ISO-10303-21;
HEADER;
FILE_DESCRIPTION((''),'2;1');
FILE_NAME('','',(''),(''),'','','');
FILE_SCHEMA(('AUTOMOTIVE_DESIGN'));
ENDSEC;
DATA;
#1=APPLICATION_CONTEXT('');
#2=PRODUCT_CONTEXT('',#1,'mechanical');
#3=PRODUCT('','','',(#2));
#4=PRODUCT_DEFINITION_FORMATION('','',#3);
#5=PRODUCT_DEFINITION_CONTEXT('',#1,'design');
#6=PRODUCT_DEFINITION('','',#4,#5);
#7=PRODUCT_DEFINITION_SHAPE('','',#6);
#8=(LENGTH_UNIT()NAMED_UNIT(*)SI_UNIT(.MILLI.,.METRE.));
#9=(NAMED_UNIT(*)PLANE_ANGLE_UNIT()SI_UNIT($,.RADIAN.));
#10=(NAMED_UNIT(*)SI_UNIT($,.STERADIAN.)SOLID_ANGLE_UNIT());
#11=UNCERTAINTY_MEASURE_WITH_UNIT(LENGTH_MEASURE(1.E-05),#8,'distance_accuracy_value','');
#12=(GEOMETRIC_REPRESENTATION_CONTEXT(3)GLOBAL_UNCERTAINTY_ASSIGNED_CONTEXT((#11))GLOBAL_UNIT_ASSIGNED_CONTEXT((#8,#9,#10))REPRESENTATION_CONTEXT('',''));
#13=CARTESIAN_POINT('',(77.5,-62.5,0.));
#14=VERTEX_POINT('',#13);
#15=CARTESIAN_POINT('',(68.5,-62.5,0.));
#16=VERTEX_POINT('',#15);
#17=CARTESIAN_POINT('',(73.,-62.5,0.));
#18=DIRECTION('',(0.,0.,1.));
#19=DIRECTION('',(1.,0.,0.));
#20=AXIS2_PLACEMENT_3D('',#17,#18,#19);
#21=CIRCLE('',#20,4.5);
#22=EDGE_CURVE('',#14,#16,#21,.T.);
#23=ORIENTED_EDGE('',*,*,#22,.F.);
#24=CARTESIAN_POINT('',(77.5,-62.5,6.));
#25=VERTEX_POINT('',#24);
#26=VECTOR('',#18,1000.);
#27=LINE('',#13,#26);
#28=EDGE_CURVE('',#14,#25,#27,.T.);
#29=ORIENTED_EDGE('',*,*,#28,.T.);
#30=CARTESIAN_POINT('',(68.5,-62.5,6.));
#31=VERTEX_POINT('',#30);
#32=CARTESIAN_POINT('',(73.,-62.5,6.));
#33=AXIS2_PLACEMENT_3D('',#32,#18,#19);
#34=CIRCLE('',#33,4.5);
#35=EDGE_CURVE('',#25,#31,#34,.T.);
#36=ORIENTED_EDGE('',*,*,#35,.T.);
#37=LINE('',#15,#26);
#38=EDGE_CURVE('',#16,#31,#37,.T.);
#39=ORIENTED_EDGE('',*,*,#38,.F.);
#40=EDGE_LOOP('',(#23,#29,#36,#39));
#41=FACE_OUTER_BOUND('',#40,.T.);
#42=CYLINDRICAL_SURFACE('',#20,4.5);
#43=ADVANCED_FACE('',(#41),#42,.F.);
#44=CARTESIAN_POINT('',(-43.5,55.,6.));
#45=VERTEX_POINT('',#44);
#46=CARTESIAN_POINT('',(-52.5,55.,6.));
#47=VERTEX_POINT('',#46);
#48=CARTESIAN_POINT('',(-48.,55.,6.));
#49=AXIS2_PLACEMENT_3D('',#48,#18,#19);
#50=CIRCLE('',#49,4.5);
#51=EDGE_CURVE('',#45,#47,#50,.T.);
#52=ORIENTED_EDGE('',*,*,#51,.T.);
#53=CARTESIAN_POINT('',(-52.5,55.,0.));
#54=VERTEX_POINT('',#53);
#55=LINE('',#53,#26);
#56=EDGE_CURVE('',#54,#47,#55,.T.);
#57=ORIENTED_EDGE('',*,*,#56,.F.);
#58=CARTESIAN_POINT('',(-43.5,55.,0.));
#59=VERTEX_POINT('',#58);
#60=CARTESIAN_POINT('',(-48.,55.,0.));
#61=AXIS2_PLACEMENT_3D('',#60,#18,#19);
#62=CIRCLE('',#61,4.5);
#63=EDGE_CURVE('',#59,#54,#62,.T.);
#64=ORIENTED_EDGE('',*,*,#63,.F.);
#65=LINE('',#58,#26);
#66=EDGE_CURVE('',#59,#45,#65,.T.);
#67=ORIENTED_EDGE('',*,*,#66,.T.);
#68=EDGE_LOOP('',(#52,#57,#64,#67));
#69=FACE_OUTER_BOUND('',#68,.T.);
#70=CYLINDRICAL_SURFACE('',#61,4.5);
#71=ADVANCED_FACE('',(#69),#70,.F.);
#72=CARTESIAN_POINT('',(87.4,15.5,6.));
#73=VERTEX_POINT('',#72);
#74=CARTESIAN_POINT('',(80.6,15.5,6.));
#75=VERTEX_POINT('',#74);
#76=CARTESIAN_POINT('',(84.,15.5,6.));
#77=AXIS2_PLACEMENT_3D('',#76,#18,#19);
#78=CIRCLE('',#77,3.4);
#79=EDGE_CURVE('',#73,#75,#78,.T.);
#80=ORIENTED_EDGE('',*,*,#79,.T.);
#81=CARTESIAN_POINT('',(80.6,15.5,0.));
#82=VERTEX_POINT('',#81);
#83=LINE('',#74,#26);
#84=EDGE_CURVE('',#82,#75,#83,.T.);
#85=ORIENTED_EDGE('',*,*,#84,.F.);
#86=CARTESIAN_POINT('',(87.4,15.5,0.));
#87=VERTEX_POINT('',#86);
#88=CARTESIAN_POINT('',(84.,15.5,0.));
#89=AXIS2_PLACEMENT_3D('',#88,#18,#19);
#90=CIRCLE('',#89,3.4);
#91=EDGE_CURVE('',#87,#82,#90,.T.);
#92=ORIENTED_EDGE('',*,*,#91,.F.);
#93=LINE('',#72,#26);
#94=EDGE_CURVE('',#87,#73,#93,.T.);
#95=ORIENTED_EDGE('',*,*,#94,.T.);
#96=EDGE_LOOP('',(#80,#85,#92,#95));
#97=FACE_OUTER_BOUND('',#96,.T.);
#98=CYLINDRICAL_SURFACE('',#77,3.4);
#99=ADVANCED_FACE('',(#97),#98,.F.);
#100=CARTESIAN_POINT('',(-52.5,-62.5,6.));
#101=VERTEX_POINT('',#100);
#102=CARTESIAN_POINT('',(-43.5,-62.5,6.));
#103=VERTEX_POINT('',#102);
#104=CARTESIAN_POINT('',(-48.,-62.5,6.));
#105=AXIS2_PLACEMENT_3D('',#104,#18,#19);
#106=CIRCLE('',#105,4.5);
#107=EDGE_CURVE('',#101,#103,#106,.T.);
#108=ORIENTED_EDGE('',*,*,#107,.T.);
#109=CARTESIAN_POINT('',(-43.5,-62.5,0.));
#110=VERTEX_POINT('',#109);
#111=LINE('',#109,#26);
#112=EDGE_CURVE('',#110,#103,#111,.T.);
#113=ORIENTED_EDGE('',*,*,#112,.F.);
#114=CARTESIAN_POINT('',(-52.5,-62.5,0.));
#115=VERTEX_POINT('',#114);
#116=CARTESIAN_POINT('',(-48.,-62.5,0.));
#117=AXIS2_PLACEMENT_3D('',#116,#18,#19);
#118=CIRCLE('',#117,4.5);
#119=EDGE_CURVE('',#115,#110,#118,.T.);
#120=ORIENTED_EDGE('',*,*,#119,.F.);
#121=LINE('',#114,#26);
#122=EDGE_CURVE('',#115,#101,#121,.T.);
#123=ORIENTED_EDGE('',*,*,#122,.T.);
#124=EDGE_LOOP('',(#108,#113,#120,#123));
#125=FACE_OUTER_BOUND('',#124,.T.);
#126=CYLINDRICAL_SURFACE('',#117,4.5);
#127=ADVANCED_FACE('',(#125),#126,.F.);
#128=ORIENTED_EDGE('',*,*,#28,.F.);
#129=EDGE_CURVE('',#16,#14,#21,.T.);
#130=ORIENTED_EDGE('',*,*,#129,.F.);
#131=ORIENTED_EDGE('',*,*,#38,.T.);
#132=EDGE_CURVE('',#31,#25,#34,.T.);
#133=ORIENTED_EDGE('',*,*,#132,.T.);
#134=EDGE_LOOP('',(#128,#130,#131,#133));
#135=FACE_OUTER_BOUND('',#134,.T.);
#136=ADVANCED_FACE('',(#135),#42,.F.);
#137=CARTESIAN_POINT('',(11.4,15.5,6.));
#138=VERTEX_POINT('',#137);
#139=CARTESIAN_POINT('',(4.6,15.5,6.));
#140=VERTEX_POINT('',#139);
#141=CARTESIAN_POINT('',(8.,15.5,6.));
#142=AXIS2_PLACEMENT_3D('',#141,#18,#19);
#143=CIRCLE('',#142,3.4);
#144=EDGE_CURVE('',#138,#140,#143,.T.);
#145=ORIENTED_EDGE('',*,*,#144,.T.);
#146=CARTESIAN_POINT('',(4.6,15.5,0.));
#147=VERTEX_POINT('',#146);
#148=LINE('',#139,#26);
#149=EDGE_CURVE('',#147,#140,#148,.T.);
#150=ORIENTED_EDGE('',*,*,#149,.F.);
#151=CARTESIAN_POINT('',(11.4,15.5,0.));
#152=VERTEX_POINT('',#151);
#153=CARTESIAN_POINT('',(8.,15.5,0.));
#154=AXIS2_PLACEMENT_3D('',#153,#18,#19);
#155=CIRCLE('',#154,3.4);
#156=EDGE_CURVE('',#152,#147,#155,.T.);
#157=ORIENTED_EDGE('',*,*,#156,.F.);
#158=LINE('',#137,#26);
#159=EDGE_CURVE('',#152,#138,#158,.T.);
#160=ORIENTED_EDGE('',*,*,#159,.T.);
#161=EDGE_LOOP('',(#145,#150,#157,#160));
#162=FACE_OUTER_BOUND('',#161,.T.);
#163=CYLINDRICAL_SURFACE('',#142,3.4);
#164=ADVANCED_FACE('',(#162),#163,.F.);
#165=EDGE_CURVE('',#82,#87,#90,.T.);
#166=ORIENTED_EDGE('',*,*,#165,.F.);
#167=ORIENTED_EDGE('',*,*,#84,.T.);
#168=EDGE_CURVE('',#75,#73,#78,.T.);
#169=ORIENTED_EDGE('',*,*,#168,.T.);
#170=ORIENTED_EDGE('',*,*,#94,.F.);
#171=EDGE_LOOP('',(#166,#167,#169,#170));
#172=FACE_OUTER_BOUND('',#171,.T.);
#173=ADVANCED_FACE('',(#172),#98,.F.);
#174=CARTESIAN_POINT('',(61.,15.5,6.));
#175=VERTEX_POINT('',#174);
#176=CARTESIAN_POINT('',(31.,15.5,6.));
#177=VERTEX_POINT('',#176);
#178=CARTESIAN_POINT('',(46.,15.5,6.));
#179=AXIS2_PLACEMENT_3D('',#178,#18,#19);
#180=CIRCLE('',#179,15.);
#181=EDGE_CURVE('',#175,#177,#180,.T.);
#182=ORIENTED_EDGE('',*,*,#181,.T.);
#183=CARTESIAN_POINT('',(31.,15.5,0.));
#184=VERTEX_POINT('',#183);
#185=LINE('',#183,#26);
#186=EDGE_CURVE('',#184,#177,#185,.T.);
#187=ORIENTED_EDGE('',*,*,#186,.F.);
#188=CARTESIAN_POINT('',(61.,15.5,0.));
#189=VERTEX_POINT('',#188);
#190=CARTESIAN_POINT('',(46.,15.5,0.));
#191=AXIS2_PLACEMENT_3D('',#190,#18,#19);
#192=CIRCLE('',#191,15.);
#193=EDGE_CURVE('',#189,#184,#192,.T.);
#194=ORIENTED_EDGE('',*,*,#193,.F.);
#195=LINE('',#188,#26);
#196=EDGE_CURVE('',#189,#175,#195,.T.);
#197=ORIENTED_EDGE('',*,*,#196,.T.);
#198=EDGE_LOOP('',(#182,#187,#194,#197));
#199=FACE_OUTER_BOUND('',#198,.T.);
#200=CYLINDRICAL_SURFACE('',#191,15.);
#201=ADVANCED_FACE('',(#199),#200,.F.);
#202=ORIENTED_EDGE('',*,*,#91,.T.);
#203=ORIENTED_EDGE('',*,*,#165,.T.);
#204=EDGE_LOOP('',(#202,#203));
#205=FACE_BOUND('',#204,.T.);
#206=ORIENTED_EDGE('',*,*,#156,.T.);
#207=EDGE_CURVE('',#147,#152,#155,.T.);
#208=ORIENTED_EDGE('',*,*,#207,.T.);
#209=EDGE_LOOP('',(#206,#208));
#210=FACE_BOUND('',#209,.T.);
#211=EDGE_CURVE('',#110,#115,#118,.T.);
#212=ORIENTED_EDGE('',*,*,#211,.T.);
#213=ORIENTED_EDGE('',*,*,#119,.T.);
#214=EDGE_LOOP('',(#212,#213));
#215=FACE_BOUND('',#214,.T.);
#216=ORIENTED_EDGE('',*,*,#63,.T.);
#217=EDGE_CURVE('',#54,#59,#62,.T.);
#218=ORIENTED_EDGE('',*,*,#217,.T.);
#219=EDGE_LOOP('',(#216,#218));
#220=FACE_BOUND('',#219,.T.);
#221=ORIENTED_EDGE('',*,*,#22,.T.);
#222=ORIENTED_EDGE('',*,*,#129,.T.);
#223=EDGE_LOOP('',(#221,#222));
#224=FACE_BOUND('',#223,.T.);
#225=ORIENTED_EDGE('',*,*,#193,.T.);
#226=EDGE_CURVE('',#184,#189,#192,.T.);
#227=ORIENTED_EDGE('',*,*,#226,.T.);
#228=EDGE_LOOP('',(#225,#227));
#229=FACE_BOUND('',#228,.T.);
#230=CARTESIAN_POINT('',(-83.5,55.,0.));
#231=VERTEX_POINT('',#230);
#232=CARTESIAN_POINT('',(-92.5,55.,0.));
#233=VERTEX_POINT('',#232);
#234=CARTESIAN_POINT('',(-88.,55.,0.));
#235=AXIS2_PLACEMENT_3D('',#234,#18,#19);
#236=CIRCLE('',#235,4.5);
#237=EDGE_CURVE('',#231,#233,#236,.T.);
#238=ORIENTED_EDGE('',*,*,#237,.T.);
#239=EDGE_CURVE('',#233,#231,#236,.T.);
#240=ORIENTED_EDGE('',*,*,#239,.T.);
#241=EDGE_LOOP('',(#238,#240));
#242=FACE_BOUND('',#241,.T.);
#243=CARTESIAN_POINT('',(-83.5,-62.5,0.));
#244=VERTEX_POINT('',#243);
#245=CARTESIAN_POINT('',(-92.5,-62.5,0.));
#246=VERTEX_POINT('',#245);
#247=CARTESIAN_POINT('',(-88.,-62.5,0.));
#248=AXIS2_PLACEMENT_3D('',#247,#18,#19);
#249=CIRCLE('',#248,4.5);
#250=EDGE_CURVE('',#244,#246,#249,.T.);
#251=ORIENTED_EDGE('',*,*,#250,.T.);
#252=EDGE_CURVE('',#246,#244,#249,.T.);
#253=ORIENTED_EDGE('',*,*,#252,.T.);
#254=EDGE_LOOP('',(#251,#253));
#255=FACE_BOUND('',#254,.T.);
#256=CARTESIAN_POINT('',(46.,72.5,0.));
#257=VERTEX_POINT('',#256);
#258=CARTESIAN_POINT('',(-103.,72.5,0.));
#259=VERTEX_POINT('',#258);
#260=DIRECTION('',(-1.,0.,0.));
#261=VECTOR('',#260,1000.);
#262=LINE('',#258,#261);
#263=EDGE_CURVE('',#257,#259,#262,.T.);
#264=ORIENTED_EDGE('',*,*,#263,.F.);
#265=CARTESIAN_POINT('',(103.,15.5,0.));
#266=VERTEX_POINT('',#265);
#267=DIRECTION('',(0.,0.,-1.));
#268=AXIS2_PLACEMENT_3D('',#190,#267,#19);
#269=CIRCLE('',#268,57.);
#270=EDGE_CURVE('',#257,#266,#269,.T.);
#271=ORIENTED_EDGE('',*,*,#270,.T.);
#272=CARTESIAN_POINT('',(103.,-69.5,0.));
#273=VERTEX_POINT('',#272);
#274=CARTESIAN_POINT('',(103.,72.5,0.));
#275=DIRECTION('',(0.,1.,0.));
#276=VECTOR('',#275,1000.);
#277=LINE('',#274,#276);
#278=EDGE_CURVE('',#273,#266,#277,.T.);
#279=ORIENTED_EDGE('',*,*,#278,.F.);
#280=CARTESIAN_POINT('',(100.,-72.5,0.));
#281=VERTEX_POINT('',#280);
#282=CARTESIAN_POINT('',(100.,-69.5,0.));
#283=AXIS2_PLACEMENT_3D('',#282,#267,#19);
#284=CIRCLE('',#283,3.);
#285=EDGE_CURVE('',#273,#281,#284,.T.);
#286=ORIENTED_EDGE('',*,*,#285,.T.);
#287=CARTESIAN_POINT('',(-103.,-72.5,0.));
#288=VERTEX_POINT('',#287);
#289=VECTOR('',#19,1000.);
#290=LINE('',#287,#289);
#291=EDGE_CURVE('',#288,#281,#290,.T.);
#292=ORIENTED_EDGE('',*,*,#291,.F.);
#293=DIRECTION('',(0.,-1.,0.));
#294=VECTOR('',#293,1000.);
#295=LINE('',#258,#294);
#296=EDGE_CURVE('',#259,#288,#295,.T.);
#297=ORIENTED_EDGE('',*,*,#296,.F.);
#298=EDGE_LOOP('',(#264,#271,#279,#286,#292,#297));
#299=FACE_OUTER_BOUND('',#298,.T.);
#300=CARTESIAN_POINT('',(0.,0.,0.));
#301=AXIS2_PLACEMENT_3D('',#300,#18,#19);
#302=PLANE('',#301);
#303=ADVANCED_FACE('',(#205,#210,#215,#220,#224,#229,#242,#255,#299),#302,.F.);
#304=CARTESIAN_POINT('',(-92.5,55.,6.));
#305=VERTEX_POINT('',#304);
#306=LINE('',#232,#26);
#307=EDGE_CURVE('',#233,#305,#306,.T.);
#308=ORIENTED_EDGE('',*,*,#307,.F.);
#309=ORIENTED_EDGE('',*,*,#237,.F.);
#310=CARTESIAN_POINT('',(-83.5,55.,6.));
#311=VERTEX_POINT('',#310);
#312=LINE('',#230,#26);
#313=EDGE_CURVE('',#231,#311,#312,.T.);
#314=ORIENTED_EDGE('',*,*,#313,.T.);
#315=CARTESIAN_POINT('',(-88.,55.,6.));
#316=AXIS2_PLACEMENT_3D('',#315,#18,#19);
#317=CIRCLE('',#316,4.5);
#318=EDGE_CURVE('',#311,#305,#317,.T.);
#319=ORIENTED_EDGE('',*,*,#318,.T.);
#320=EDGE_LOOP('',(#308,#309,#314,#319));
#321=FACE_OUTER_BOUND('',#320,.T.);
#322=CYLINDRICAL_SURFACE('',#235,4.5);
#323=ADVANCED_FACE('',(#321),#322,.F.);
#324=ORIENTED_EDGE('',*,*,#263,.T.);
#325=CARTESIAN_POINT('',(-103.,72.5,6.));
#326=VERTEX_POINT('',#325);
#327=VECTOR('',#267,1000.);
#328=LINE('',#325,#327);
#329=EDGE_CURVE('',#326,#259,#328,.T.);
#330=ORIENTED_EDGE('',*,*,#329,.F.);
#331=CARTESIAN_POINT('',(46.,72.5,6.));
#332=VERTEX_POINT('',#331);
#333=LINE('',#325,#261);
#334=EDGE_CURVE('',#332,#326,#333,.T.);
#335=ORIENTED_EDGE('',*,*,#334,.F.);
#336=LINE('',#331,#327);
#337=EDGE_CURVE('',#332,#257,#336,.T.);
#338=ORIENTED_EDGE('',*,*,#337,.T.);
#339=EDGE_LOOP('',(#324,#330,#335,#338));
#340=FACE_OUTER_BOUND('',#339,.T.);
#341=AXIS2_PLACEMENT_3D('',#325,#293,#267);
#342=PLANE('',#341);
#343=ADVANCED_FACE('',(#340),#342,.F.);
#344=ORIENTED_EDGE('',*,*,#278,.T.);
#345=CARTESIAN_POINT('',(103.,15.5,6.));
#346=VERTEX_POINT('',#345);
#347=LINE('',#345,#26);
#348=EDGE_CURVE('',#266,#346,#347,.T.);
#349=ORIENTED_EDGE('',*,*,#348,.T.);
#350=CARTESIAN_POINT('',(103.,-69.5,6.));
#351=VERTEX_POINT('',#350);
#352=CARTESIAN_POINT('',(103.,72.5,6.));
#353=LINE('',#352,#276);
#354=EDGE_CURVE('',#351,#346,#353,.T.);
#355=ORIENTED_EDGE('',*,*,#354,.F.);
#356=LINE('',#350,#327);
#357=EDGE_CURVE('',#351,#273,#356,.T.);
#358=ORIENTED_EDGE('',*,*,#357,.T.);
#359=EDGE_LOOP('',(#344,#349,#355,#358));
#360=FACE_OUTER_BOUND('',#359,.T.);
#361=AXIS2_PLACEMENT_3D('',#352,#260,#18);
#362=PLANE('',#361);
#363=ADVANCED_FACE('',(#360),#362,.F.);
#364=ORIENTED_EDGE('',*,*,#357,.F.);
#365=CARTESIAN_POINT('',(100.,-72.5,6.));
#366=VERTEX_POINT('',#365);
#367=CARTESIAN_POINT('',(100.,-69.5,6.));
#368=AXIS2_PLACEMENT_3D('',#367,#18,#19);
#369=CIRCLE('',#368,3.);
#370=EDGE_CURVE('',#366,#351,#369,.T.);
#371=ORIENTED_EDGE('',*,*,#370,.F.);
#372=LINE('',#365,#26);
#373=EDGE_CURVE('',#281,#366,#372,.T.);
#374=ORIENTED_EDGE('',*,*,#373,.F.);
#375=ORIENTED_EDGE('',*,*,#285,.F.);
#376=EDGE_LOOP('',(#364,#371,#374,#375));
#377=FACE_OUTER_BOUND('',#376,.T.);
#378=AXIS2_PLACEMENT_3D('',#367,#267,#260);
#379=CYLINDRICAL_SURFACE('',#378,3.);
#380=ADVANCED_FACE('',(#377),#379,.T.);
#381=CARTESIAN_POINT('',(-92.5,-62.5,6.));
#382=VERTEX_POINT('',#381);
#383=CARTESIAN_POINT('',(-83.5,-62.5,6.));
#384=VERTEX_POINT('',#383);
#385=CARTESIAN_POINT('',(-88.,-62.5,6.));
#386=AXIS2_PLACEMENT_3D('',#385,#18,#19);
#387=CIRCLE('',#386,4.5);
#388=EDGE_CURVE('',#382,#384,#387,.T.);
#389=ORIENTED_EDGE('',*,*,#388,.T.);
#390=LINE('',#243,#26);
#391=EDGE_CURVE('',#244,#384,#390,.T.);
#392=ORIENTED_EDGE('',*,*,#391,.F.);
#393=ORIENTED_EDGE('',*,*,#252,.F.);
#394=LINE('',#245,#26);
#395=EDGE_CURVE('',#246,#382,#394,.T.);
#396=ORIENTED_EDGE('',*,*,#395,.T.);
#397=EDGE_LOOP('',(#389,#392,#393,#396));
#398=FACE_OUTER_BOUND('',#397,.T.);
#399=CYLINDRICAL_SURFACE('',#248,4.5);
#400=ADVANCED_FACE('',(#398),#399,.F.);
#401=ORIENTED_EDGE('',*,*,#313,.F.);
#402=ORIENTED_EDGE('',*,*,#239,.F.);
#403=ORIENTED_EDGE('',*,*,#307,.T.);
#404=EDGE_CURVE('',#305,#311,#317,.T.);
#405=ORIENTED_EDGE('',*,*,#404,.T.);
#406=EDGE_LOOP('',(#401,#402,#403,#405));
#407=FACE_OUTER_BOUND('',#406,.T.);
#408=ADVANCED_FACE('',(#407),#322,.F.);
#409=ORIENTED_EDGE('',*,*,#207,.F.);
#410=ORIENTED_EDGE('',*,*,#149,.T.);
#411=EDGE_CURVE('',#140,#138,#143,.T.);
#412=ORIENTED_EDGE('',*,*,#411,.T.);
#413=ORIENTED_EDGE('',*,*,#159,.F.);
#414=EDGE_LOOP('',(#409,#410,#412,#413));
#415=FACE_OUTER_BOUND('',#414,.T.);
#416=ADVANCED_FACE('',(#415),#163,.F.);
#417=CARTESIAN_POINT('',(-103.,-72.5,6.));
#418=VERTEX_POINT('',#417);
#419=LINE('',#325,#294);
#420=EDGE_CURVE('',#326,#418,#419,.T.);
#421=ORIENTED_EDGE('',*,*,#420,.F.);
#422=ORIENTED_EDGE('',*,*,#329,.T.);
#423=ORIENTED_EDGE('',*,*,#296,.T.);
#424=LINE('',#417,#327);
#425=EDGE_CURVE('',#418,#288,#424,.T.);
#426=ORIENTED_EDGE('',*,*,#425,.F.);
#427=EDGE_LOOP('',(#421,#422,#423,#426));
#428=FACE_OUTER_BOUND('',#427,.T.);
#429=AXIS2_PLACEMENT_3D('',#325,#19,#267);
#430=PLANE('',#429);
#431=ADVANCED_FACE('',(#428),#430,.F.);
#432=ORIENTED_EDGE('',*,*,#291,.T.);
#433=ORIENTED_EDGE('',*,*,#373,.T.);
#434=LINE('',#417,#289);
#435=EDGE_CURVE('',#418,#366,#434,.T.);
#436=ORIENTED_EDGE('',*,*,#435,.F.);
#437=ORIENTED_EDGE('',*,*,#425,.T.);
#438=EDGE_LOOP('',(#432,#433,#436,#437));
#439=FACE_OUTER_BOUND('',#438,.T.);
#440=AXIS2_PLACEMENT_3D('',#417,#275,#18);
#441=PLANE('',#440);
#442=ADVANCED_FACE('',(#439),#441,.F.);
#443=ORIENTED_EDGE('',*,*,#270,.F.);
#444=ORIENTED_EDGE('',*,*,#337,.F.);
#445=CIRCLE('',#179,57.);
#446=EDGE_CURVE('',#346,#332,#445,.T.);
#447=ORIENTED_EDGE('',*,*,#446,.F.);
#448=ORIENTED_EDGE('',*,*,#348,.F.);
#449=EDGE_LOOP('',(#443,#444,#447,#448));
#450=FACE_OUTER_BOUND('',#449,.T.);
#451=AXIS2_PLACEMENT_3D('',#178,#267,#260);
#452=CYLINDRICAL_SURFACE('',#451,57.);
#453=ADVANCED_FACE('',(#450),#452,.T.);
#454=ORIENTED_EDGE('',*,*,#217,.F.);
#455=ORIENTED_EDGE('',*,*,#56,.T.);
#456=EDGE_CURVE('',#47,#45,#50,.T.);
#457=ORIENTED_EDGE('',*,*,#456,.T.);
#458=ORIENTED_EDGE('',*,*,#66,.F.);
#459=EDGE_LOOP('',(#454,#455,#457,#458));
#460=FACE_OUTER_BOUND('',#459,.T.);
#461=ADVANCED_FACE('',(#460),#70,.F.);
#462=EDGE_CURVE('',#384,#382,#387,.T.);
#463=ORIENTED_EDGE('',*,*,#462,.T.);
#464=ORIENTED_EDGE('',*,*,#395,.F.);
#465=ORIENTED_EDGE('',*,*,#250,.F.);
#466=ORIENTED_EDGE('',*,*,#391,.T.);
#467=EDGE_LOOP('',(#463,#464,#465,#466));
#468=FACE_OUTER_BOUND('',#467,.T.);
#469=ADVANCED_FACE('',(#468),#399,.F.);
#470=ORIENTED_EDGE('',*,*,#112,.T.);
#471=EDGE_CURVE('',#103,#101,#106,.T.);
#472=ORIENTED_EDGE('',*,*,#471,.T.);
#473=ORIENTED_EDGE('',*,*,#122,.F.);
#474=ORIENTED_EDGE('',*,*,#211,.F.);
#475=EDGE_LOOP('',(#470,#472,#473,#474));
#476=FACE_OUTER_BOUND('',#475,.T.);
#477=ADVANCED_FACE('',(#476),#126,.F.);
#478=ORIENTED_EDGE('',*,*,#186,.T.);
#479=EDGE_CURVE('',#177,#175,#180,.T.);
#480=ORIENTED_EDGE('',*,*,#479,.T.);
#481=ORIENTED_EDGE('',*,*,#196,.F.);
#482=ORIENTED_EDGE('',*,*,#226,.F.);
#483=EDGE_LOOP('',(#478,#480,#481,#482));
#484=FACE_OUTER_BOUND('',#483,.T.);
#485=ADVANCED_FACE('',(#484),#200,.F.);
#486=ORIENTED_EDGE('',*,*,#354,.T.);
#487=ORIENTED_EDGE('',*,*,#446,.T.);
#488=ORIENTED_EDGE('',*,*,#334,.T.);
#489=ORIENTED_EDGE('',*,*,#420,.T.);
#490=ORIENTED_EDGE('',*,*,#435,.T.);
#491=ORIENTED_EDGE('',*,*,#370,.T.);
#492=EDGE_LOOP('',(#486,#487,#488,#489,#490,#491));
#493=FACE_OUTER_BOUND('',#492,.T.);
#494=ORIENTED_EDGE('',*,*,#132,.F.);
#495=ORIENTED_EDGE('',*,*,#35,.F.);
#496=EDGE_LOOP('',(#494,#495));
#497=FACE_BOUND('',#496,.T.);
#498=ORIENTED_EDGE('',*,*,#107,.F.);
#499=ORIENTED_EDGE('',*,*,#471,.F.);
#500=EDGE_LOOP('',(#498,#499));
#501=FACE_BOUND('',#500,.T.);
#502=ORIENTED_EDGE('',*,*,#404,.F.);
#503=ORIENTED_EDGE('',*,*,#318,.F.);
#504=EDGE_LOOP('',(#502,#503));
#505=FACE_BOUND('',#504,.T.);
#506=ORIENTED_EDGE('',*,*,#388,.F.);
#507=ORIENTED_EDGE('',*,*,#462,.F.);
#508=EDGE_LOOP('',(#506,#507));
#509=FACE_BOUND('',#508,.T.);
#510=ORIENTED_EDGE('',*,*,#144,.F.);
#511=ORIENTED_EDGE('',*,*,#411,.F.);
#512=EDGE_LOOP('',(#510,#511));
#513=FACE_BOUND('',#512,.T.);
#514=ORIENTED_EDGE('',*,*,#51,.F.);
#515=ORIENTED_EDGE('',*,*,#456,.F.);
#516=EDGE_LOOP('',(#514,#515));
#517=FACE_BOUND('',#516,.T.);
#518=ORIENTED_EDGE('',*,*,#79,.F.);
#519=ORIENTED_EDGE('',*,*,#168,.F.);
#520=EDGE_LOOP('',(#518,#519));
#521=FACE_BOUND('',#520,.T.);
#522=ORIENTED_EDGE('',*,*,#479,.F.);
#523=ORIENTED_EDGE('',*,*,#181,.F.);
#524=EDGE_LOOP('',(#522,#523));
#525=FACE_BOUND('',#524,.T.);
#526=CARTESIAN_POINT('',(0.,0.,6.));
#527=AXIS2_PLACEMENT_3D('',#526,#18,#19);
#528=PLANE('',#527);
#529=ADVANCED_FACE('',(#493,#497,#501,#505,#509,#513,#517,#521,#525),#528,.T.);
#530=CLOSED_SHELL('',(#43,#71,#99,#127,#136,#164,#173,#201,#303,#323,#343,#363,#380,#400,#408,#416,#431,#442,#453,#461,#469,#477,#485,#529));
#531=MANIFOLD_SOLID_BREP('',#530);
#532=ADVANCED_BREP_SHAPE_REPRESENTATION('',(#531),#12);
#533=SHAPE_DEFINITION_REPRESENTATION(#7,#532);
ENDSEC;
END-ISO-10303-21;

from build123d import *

# Parameters (mm, degrees)
SKETCH_1_W               = 206
SKETCH_1_H               = 145
EXTRUDE_1_DEPTH          = 6
SKETCH_3_R               = 4.5
CUT_EXTRUDE_2_DEPTH      = 127.100158604
SKETCH_4_R               = 15
CUT_EXTRUDE_3_DEPTH      = 127.100158604
FILLET_1_R               = 57
HOLE_WIZARD_M8_1_D       = 6.8
PATTERN_CIRCULAR_1_COUNT = 2
SKETCH_11_R              = 4.5
CUT_EXTRUDE_6_DEPTH      = 127.100158604
FILLET_5_R               = 3


with BuildPart() as part:
    # 草图1 → 凸台-拉伸1 (new body)
    with BuildSketch(Plane.XY):
        Rectangle(SKETCH_1_W, SKETCH_1_H)
    extrude(amount=EXTRUDE_1_DEPTH)

    # 草图3 → 切除-拉伸2 (cut, through all)
    with BuildSketch(Plane.XY.offset(6)):
        with Locations((-88, 55)):
            Circle(SKETCH_3_R)
        with Locations((-48, 55)):
            Circle(SKETCH_3_R)
        with Locations((-88, -62.5)):
            Circle(SKETCH_3_R)
        with Locations((-48, -62.5)):
            Circle(SKETCH_3_R)
    extrude(amount=-CUT_EXTRUDE_2_DEPTH, mode=Mode.SUBTRACT)

    # 草图4 → 切除-拉伸3 (cut, through all)
    with BuildSketch(Plane.XY.offset(6)):
        with Locations((46, 15.5)):
            Circle(SKETCH_4_R)
    extrude(amount=-CUT_EXTRUDE_3_DEPTH, mode=Mode.SUBTRACT)

    # 圆角1
    fillet_1_edges = [part.edges().sort_by_distance(p)[0] for p in [
        (103, 72.5, 3),
    ]]
    fillet(fillet_1_edges, radius=FILLET_1_R)

    # M8 螺纹孔1 (through all)
    with Locations(Plane.XY.offset(6)):
        with Locations((8, 15.5)):
            hole_wizard_m8_1 = Hole(HOLE_WIZARD_M8_1_D / 2)

    # 阵列(圆周)1: M8 螺纹孔1 ×2 about axis
    pattern_circular_1_axis = Axis((46, 15.5, 0), (0, 0, 1))
    for i in range(1, PATTERN_CIRCULAR_1_COUNT):
        add(hole_wizard_m8_1.rotate(pattern_circular_1_axis, i * 360 / PATTERN_CIRCULAR_1_COUNT), mode=Mode.SUBTRACT)

    # 草图11 → 切除-拉伸6 (cut, through all)
    with BuildSketch(Plane.XY.offset(6)):
        with Locations((73, -62.5)):
            Circle(SKETCH_11_R)
    extrude(amount=-CUT_EXTRUDE_6_DEPTH, mode=Mode.SUBTRACT)

    # 圆角5
    fillet_5_edges = [part.edges().sort_by_distance(p)[0] for p in [
        (103, -72.5, 3),
    ]]
    fillet(fillet_5_edges, radius=FILLET_5_R)


solid = part.part
